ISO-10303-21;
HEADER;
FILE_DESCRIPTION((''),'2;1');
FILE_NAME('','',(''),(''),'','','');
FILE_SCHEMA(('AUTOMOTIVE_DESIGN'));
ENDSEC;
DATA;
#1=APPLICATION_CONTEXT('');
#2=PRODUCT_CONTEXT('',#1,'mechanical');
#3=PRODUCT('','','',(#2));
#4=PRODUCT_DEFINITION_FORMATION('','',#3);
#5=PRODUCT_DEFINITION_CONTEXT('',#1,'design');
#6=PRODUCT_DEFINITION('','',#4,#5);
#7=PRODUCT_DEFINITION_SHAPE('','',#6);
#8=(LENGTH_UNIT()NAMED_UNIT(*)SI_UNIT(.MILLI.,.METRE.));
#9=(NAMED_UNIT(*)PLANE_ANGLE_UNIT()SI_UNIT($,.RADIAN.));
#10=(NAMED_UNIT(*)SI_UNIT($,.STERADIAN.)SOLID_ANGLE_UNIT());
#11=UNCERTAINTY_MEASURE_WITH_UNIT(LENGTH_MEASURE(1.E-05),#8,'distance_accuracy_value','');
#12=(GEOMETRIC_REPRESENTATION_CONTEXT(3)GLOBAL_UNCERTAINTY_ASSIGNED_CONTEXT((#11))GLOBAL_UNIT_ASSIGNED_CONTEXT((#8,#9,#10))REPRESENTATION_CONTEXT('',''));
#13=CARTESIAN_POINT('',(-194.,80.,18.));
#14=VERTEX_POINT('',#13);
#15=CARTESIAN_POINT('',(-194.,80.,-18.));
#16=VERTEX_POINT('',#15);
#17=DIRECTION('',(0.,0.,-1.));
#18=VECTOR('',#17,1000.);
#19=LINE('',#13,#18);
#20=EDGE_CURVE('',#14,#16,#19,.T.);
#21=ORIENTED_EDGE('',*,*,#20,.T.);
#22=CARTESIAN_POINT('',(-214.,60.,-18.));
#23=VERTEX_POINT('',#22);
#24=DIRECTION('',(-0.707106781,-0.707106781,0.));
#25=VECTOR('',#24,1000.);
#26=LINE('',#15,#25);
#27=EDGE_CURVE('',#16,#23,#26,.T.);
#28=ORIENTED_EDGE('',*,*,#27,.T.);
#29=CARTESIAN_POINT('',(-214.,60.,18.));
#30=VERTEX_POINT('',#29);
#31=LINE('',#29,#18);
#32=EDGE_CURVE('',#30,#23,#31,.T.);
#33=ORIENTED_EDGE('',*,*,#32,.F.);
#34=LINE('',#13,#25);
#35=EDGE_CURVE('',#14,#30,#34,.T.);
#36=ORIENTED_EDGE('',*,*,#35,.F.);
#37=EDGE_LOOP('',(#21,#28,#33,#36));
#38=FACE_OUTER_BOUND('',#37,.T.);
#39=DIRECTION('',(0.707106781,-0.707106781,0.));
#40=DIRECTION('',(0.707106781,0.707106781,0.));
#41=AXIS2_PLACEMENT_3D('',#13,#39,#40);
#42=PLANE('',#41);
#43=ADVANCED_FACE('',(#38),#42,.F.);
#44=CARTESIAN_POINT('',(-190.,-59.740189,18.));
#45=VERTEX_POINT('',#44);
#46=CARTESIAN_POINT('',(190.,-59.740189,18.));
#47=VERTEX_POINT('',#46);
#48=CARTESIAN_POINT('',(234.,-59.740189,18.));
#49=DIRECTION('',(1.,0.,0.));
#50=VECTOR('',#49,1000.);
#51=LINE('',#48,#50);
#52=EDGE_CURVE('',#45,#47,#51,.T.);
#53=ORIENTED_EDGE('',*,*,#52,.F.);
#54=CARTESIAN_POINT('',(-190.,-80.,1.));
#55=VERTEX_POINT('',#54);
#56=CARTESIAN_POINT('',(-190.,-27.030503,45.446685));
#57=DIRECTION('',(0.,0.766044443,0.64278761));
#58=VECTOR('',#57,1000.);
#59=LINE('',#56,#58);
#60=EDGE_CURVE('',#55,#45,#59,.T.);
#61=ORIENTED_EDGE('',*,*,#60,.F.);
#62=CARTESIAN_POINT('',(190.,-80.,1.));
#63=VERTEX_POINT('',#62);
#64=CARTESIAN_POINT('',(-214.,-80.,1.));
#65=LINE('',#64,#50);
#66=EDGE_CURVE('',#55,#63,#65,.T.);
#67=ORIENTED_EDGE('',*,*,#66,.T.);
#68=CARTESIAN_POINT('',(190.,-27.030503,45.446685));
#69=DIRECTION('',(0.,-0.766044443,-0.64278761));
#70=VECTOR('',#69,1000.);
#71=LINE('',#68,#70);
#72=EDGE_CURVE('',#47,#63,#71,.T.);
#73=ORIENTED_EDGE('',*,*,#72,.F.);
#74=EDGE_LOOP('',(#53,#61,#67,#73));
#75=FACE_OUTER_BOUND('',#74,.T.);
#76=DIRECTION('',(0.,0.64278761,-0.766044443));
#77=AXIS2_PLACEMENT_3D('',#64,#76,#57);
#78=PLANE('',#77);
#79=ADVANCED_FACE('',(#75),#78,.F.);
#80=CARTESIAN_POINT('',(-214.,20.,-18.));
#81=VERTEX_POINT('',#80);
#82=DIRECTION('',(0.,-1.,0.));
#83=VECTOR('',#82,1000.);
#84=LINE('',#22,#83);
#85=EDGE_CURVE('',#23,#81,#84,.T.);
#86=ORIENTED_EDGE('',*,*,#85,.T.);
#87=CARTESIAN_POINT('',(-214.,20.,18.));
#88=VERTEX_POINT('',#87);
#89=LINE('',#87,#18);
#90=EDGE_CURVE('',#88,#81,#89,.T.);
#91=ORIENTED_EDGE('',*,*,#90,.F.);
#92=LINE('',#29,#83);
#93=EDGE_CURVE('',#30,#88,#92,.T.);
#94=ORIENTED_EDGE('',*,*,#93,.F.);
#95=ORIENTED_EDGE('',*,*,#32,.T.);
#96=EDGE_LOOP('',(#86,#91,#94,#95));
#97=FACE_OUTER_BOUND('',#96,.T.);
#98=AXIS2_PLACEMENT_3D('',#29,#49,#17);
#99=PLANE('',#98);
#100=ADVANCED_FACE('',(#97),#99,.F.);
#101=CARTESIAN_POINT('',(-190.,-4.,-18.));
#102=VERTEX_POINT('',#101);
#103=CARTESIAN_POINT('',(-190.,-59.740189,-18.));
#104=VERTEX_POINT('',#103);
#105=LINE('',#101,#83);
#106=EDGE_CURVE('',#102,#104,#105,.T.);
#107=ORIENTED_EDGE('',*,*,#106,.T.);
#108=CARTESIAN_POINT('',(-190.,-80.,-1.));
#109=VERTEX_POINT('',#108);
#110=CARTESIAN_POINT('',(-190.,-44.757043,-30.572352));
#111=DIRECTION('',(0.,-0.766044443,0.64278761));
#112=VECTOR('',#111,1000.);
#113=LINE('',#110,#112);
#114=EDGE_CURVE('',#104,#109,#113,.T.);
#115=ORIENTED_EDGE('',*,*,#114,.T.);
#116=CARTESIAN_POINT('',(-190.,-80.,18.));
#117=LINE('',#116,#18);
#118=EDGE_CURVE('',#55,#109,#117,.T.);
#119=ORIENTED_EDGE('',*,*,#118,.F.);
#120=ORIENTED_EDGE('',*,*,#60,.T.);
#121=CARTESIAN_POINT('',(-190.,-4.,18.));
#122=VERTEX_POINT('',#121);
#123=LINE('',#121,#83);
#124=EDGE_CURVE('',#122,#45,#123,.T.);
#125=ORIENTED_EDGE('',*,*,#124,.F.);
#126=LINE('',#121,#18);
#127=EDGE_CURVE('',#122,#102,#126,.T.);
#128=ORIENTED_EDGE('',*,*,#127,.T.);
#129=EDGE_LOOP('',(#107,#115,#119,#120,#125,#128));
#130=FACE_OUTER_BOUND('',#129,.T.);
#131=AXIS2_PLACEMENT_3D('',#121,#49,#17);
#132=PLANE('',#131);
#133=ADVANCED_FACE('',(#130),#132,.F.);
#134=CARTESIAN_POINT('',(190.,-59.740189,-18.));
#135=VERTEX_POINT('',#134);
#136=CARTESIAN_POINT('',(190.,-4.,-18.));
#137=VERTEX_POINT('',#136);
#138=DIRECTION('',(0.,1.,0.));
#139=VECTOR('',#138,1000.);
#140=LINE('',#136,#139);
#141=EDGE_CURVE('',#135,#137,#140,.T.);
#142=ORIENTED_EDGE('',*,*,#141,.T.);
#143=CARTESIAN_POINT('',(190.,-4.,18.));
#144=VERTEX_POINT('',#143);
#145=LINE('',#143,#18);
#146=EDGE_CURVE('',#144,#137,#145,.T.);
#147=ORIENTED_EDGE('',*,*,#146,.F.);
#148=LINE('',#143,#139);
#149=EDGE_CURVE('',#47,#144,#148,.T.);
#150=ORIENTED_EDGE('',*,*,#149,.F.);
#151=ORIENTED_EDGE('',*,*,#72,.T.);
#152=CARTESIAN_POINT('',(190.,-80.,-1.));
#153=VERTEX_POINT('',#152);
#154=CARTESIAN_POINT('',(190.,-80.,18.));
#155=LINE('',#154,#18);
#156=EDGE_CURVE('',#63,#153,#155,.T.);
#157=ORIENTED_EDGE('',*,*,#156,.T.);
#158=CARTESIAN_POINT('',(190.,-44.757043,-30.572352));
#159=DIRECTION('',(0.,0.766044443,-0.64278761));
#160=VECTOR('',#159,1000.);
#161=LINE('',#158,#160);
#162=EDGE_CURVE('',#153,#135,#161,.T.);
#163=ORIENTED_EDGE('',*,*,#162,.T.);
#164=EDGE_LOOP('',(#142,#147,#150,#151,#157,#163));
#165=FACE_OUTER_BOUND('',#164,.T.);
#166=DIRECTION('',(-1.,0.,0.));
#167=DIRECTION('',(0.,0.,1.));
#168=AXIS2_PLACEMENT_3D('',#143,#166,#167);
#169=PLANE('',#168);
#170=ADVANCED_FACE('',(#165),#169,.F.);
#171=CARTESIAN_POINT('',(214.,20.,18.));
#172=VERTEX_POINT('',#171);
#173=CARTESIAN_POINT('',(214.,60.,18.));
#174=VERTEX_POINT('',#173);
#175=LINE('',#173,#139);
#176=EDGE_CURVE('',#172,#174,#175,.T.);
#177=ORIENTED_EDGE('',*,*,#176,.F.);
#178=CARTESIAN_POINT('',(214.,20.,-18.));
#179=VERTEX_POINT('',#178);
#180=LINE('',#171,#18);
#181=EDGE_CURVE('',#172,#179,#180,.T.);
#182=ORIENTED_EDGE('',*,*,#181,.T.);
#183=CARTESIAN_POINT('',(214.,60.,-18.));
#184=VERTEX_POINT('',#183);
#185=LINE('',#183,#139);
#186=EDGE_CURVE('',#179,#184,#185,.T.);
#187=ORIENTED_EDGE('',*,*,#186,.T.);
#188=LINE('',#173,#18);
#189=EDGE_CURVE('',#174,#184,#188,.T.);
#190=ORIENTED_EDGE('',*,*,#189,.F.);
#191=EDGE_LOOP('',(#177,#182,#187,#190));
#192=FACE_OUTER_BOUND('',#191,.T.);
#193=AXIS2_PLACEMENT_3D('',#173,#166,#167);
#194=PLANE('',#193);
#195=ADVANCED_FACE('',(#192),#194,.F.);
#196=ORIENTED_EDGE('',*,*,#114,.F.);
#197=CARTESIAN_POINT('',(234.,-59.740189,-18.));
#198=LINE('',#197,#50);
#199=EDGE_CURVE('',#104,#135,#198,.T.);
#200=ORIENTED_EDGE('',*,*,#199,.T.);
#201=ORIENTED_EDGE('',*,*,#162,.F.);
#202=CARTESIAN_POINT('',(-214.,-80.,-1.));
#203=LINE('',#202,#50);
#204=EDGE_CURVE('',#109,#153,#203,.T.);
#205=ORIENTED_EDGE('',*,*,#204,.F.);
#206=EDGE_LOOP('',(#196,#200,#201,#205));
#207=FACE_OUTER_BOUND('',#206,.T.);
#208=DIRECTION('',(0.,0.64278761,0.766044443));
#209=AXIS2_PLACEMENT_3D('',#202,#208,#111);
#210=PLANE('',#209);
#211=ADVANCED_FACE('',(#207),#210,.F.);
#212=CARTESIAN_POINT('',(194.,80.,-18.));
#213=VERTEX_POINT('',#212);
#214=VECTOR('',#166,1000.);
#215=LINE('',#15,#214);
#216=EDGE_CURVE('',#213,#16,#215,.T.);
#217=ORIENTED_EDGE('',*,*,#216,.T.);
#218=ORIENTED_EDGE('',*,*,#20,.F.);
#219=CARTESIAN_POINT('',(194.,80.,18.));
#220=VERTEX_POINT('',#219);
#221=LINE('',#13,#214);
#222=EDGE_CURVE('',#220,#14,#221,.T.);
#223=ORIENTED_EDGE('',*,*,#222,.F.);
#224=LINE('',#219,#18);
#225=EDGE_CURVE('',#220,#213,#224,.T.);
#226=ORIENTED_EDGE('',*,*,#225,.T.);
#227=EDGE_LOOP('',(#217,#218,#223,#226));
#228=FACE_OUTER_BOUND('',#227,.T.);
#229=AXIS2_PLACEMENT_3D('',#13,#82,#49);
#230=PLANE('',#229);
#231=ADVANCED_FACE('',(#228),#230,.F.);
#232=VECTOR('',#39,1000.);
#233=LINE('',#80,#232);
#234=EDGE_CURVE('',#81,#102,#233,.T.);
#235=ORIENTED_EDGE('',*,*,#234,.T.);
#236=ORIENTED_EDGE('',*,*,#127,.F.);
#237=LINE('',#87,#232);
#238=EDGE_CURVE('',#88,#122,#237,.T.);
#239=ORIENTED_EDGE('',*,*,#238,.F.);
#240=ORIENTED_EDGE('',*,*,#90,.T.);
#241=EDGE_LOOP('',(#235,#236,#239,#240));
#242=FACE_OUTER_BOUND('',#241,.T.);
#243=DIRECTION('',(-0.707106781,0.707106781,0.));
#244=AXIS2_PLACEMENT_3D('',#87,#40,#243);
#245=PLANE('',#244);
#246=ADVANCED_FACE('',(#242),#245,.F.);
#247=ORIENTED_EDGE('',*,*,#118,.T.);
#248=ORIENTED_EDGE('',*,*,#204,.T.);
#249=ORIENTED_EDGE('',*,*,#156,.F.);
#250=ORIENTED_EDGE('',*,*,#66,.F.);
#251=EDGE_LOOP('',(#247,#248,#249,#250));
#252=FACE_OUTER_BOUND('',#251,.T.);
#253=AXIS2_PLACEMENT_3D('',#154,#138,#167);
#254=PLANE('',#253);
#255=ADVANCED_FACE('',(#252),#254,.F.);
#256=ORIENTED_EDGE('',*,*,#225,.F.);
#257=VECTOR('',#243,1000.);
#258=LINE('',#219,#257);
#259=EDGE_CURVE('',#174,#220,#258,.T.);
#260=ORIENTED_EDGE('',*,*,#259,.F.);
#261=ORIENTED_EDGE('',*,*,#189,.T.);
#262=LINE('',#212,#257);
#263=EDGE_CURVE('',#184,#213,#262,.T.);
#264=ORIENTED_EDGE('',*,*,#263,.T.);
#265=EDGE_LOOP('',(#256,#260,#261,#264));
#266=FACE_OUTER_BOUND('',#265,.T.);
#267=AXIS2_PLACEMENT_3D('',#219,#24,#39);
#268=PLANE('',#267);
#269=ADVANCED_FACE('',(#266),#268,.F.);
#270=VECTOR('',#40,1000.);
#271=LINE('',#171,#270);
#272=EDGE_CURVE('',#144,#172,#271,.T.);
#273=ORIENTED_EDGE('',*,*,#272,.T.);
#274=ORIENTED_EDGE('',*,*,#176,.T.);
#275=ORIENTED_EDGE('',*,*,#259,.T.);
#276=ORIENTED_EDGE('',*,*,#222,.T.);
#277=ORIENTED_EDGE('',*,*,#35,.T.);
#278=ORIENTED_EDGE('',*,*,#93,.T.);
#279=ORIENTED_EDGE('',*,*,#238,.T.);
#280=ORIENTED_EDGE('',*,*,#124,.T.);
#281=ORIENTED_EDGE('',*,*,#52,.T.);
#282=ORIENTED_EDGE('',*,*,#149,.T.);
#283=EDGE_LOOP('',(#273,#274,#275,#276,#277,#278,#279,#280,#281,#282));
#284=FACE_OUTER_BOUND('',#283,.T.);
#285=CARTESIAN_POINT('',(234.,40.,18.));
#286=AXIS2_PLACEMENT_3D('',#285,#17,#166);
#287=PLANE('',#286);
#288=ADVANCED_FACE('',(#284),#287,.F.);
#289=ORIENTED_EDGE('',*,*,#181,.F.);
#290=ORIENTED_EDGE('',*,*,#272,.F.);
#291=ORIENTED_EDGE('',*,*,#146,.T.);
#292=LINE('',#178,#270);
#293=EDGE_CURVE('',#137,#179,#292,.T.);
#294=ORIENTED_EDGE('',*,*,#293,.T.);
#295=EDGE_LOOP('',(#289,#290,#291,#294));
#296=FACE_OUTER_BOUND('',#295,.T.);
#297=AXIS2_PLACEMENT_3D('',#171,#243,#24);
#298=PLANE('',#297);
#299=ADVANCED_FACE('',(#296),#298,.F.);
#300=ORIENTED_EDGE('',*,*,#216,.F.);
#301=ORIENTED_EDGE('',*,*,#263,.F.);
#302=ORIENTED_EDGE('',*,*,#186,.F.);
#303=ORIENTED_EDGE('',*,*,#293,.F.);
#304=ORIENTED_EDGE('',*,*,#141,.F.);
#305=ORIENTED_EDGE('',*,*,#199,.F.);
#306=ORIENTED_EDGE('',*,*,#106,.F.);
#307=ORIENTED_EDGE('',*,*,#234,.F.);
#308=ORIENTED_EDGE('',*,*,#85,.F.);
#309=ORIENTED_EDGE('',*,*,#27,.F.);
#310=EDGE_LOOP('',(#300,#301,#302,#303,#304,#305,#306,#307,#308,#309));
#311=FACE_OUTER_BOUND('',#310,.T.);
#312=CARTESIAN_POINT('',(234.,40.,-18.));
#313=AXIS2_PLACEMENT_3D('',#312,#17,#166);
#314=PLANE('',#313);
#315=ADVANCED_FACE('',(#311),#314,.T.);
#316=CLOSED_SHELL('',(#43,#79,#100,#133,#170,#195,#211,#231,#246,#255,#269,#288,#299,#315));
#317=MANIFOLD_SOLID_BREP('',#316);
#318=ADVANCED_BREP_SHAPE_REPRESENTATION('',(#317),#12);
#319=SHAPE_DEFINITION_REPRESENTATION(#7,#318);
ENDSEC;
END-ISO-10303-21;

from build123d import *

# Parameters (mm, degrees)
BOSS_EXTRUDE1_DEPTH = 18
CUT_EXTRUDE1_DEPTH  = 214


with BuildPart() as part:
    # Sketch1 → Boss-Extrude1 (new, symmetric)
    with BuildSketch(Plane.XY):
        Polygon((-194, 80), (194, 80), (214, 60), (214, 20), (190, -4), (190, -80), (-190, -80), (-190, -4), (-214, 20), (-214, 60), align=None)
    extrude(amount=BOSS_EXTRUDE1_DEPTH, both=True)

    # Sketch2 → Cut-Extrude1 (cut, symmetric)
    with BuildSketch(Plane(origin=(0, 0, 0), x_dir=(0, 0, -1), z_dir=(1, 0, 0))):
        Polygon((-1, -80), (-18, -59.740188926), (-18, -80), align=None)
        Polygon((1, -80), (18, -59.740188926), (18, -80), align=None)
    extrude(amount=CUT_EXTRUDE1_DEPTH, both=True, mode=Mode.SUBTRACT)


solid = part.part
